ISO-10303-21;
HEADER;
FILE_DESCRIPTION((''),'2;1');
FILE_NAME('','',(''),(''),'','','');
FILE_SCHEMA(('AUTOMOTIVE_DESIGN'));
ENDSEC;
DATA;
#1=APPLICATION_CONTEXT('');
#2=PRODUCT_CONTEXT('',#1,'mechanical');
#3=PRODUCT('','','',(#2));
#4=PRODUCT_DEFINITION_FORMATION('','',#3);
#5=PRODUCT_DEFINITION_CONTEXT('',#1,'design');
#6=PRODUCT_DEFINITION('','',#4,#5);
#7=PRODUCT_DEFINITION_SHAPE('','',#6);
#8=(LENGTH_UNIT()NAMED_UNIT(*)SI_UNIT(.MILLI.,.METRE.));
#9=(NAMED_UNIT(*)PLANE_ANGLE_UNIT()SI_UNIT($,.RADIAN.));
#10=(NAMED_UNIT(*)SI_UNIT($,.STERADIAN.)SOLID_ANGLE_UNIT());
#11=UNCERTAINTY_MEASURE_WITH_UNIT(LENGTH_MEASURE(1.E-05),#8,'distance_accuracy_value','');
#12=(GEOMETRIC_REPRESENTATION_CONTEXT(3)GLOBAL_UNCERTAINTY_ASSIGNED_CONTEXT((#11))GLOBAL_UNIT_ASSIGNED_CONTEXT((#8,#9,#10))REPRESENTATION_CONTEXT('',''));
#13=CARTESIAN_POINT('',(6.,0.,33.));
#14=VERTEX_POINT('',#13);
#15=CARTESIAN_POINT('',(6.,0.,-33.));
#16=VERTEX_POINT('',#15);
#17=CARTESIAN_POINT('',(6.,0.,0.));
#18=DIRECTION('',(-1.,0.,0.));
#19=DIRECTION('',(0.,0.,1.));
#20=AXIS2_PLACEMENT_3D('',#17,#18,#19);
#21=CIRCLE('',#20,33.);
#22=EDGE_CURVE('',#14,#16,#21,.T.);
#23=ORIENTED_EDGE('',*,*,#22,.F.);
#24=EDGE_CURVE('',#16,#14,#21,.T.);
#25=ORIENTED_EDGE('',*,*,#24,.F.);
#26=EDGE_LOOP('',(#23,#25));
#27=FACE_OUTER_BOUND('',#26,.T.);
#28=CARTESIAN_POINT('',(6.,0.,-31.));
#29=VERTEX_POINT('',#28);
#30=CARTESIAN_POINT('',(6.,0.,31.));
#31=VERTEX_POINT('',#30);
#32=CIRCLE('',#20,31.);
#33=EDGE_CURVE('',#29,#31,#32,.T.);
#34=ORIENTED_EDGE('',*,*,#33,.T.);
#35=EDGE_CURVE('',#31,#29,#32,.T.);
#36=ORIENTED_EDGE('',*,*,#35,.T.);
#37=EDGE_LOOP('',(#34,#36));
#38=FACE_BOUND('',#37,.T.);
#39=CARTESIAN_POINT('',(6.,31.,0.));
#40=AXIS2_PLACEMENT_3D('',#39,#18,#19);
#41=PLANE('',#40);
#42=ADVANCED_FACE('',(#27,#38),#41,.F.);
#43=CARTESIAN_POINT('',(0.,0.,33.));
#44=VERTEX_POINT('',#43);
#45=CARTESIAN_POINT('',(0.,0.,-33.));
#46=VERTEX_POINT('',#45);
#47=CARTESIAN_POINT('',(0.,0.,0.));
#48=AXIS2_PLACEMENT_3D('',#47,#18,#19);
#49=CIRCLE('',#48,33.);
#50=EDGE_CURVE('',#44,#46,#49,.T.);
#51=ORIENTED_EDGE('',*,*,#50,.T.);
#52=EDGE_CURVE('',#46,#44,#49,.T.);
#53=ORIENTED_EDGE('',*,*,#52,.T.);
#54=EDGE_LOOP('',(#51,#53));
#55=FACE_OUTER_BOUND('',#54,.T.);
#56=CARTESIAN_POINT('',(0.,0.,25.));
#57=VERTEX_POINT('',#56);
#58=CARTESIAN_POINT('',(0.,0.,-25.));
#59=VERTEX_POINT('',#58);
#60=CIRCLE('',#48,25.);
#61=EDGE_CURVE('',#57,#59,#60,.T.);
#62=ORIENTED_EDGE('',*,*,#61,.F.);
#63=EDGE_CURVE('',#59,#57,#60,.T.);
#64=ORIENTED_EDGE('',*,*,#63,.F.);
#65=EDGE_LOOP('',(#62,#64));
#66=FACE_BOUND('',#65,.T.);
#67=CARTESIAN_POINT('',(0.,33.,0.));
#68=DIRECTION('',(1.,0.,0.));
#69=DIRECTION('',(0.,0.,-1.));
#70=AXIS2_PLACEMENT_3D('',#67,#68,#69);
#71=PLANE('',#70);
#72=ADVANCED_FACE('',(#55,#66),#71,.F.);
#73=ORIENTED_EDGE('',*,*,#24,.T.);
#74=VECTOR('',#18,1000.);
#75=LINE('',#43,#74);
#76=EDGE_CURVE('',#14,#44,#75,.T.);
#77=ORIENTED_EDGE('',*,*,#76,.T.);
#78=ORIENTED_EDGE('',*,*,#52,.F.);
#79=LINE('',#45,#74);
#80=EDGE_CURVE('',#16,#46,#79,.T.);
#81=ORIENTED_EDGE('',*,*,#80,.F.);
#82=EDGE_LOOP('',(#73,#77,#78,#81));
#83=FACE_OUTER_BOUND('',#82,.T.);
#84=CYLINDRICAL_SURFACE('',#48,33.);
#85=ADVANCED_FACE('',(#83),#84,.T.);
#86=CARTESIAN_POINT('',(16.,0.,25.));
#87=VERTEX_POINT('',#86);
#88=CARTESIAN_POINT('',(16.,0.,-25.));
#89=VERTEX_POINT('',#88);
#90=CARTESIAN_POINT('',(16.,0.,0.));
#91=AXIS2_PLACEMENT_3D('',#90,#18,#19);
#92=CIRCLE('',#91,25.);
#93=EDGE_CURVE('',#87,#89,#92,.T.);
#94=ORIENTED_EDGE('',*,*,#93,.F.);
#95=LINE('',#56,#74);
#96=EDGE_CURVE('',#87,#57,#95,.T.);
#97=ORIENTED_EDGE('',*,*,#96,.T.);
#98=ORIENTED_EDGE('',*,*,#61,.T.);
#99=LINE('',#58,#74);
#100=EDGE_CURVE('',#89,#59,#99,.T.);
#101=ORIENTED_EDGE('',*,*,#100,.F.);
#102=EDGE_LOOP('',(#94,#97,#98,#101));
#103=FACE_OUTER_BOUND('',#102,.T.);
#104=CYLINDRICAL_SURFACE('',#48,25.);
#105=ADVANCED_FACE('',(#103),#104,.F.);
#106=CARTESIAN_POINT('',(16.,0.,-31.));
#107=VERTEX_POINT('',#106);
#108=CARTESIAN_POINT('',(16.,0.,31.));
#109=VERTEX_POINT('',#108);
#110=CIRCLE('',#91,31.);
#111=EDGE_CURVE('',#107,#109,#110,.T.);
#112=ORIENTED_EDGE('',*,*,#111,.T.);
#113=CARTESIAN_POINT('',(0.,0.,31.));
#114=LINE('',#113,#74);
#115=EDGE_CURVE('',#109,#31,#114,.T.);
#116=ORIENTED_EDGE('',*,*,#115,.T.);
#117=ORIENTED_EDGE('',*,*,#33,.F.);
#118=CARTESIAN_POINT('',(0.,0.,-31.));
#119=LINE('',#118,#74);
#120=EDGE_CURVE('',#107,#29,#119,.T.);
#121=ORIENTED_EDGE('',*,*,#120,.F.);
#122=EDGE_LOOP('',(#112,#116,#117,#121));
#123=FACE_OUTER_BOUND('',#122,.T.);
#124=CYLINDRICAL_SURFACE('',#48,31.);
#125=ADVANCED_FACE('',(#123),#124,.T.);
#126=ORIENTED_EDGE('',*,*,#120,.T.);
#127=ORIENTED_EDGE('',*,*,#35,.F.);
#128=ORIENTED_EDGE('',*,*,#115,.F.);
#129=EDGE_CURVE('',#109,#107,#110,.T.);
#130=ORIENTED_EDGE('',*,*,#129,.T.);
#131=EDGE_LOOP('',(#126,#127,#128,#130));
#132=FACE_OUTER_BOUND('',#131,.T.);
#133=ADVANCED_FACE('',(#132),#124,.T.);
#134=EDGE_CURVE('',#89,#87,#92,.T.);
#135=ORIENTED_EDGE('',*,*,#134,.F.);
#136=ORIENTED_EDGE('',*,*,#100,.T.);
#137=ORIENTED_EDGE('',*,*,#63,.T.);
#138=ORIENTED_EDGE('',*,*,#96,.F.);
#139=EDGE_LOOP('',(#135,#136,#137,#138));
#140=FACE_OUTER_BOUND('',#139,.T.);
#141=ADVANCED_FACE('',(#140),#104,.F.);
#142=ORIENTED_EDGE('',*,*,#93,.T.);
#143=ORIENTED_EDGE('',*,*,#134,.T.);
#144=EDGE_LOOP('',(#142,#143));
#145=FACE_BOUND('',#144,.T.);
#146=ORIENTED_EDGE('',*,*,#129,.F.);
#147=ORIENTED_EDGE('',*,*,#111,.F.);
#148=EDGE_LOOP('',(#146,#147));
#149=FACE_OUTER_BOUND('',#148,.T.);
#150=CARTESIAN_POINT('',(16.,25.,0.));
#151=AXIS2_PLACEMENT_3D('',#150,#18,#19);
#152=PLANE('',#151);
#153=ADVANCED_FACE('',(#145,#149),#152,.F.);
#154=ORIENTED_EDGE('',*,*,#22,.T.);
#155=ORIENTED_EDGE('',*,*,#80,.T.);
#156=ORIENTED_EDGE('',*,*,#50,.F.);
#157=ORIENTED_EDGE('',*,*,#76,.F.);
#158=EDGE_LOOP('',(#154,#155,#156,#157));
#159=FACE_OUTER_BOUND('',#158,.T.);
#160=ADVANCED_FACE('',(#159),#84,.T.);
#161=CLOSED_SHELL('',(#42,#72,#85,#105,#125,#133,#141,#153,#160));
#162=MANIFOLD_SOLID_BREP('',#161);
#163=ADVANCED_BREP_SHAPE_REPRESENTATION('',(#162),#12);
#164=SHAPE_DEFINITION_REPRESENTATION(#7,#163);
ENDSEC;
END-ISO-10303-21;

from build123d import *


with BuildPart() as part:
    # Sketch1 → Revolve1 (revolve)
    with BuildSketch(Plane.XY, mode=Mode.PRIVATE) as revolve1_sk:
        Polygon((0, 25), (16, 25), (16, 31), (6, 31), (6, 33), (0, 33), align=None)
    revolve(revolve1_sk.sketch.rotate(Axis((0, 0, 0), (1, 0, 0)), 90), axis=Axis((0, 0, 0), (1, 0, 0)))


solid = part.part
